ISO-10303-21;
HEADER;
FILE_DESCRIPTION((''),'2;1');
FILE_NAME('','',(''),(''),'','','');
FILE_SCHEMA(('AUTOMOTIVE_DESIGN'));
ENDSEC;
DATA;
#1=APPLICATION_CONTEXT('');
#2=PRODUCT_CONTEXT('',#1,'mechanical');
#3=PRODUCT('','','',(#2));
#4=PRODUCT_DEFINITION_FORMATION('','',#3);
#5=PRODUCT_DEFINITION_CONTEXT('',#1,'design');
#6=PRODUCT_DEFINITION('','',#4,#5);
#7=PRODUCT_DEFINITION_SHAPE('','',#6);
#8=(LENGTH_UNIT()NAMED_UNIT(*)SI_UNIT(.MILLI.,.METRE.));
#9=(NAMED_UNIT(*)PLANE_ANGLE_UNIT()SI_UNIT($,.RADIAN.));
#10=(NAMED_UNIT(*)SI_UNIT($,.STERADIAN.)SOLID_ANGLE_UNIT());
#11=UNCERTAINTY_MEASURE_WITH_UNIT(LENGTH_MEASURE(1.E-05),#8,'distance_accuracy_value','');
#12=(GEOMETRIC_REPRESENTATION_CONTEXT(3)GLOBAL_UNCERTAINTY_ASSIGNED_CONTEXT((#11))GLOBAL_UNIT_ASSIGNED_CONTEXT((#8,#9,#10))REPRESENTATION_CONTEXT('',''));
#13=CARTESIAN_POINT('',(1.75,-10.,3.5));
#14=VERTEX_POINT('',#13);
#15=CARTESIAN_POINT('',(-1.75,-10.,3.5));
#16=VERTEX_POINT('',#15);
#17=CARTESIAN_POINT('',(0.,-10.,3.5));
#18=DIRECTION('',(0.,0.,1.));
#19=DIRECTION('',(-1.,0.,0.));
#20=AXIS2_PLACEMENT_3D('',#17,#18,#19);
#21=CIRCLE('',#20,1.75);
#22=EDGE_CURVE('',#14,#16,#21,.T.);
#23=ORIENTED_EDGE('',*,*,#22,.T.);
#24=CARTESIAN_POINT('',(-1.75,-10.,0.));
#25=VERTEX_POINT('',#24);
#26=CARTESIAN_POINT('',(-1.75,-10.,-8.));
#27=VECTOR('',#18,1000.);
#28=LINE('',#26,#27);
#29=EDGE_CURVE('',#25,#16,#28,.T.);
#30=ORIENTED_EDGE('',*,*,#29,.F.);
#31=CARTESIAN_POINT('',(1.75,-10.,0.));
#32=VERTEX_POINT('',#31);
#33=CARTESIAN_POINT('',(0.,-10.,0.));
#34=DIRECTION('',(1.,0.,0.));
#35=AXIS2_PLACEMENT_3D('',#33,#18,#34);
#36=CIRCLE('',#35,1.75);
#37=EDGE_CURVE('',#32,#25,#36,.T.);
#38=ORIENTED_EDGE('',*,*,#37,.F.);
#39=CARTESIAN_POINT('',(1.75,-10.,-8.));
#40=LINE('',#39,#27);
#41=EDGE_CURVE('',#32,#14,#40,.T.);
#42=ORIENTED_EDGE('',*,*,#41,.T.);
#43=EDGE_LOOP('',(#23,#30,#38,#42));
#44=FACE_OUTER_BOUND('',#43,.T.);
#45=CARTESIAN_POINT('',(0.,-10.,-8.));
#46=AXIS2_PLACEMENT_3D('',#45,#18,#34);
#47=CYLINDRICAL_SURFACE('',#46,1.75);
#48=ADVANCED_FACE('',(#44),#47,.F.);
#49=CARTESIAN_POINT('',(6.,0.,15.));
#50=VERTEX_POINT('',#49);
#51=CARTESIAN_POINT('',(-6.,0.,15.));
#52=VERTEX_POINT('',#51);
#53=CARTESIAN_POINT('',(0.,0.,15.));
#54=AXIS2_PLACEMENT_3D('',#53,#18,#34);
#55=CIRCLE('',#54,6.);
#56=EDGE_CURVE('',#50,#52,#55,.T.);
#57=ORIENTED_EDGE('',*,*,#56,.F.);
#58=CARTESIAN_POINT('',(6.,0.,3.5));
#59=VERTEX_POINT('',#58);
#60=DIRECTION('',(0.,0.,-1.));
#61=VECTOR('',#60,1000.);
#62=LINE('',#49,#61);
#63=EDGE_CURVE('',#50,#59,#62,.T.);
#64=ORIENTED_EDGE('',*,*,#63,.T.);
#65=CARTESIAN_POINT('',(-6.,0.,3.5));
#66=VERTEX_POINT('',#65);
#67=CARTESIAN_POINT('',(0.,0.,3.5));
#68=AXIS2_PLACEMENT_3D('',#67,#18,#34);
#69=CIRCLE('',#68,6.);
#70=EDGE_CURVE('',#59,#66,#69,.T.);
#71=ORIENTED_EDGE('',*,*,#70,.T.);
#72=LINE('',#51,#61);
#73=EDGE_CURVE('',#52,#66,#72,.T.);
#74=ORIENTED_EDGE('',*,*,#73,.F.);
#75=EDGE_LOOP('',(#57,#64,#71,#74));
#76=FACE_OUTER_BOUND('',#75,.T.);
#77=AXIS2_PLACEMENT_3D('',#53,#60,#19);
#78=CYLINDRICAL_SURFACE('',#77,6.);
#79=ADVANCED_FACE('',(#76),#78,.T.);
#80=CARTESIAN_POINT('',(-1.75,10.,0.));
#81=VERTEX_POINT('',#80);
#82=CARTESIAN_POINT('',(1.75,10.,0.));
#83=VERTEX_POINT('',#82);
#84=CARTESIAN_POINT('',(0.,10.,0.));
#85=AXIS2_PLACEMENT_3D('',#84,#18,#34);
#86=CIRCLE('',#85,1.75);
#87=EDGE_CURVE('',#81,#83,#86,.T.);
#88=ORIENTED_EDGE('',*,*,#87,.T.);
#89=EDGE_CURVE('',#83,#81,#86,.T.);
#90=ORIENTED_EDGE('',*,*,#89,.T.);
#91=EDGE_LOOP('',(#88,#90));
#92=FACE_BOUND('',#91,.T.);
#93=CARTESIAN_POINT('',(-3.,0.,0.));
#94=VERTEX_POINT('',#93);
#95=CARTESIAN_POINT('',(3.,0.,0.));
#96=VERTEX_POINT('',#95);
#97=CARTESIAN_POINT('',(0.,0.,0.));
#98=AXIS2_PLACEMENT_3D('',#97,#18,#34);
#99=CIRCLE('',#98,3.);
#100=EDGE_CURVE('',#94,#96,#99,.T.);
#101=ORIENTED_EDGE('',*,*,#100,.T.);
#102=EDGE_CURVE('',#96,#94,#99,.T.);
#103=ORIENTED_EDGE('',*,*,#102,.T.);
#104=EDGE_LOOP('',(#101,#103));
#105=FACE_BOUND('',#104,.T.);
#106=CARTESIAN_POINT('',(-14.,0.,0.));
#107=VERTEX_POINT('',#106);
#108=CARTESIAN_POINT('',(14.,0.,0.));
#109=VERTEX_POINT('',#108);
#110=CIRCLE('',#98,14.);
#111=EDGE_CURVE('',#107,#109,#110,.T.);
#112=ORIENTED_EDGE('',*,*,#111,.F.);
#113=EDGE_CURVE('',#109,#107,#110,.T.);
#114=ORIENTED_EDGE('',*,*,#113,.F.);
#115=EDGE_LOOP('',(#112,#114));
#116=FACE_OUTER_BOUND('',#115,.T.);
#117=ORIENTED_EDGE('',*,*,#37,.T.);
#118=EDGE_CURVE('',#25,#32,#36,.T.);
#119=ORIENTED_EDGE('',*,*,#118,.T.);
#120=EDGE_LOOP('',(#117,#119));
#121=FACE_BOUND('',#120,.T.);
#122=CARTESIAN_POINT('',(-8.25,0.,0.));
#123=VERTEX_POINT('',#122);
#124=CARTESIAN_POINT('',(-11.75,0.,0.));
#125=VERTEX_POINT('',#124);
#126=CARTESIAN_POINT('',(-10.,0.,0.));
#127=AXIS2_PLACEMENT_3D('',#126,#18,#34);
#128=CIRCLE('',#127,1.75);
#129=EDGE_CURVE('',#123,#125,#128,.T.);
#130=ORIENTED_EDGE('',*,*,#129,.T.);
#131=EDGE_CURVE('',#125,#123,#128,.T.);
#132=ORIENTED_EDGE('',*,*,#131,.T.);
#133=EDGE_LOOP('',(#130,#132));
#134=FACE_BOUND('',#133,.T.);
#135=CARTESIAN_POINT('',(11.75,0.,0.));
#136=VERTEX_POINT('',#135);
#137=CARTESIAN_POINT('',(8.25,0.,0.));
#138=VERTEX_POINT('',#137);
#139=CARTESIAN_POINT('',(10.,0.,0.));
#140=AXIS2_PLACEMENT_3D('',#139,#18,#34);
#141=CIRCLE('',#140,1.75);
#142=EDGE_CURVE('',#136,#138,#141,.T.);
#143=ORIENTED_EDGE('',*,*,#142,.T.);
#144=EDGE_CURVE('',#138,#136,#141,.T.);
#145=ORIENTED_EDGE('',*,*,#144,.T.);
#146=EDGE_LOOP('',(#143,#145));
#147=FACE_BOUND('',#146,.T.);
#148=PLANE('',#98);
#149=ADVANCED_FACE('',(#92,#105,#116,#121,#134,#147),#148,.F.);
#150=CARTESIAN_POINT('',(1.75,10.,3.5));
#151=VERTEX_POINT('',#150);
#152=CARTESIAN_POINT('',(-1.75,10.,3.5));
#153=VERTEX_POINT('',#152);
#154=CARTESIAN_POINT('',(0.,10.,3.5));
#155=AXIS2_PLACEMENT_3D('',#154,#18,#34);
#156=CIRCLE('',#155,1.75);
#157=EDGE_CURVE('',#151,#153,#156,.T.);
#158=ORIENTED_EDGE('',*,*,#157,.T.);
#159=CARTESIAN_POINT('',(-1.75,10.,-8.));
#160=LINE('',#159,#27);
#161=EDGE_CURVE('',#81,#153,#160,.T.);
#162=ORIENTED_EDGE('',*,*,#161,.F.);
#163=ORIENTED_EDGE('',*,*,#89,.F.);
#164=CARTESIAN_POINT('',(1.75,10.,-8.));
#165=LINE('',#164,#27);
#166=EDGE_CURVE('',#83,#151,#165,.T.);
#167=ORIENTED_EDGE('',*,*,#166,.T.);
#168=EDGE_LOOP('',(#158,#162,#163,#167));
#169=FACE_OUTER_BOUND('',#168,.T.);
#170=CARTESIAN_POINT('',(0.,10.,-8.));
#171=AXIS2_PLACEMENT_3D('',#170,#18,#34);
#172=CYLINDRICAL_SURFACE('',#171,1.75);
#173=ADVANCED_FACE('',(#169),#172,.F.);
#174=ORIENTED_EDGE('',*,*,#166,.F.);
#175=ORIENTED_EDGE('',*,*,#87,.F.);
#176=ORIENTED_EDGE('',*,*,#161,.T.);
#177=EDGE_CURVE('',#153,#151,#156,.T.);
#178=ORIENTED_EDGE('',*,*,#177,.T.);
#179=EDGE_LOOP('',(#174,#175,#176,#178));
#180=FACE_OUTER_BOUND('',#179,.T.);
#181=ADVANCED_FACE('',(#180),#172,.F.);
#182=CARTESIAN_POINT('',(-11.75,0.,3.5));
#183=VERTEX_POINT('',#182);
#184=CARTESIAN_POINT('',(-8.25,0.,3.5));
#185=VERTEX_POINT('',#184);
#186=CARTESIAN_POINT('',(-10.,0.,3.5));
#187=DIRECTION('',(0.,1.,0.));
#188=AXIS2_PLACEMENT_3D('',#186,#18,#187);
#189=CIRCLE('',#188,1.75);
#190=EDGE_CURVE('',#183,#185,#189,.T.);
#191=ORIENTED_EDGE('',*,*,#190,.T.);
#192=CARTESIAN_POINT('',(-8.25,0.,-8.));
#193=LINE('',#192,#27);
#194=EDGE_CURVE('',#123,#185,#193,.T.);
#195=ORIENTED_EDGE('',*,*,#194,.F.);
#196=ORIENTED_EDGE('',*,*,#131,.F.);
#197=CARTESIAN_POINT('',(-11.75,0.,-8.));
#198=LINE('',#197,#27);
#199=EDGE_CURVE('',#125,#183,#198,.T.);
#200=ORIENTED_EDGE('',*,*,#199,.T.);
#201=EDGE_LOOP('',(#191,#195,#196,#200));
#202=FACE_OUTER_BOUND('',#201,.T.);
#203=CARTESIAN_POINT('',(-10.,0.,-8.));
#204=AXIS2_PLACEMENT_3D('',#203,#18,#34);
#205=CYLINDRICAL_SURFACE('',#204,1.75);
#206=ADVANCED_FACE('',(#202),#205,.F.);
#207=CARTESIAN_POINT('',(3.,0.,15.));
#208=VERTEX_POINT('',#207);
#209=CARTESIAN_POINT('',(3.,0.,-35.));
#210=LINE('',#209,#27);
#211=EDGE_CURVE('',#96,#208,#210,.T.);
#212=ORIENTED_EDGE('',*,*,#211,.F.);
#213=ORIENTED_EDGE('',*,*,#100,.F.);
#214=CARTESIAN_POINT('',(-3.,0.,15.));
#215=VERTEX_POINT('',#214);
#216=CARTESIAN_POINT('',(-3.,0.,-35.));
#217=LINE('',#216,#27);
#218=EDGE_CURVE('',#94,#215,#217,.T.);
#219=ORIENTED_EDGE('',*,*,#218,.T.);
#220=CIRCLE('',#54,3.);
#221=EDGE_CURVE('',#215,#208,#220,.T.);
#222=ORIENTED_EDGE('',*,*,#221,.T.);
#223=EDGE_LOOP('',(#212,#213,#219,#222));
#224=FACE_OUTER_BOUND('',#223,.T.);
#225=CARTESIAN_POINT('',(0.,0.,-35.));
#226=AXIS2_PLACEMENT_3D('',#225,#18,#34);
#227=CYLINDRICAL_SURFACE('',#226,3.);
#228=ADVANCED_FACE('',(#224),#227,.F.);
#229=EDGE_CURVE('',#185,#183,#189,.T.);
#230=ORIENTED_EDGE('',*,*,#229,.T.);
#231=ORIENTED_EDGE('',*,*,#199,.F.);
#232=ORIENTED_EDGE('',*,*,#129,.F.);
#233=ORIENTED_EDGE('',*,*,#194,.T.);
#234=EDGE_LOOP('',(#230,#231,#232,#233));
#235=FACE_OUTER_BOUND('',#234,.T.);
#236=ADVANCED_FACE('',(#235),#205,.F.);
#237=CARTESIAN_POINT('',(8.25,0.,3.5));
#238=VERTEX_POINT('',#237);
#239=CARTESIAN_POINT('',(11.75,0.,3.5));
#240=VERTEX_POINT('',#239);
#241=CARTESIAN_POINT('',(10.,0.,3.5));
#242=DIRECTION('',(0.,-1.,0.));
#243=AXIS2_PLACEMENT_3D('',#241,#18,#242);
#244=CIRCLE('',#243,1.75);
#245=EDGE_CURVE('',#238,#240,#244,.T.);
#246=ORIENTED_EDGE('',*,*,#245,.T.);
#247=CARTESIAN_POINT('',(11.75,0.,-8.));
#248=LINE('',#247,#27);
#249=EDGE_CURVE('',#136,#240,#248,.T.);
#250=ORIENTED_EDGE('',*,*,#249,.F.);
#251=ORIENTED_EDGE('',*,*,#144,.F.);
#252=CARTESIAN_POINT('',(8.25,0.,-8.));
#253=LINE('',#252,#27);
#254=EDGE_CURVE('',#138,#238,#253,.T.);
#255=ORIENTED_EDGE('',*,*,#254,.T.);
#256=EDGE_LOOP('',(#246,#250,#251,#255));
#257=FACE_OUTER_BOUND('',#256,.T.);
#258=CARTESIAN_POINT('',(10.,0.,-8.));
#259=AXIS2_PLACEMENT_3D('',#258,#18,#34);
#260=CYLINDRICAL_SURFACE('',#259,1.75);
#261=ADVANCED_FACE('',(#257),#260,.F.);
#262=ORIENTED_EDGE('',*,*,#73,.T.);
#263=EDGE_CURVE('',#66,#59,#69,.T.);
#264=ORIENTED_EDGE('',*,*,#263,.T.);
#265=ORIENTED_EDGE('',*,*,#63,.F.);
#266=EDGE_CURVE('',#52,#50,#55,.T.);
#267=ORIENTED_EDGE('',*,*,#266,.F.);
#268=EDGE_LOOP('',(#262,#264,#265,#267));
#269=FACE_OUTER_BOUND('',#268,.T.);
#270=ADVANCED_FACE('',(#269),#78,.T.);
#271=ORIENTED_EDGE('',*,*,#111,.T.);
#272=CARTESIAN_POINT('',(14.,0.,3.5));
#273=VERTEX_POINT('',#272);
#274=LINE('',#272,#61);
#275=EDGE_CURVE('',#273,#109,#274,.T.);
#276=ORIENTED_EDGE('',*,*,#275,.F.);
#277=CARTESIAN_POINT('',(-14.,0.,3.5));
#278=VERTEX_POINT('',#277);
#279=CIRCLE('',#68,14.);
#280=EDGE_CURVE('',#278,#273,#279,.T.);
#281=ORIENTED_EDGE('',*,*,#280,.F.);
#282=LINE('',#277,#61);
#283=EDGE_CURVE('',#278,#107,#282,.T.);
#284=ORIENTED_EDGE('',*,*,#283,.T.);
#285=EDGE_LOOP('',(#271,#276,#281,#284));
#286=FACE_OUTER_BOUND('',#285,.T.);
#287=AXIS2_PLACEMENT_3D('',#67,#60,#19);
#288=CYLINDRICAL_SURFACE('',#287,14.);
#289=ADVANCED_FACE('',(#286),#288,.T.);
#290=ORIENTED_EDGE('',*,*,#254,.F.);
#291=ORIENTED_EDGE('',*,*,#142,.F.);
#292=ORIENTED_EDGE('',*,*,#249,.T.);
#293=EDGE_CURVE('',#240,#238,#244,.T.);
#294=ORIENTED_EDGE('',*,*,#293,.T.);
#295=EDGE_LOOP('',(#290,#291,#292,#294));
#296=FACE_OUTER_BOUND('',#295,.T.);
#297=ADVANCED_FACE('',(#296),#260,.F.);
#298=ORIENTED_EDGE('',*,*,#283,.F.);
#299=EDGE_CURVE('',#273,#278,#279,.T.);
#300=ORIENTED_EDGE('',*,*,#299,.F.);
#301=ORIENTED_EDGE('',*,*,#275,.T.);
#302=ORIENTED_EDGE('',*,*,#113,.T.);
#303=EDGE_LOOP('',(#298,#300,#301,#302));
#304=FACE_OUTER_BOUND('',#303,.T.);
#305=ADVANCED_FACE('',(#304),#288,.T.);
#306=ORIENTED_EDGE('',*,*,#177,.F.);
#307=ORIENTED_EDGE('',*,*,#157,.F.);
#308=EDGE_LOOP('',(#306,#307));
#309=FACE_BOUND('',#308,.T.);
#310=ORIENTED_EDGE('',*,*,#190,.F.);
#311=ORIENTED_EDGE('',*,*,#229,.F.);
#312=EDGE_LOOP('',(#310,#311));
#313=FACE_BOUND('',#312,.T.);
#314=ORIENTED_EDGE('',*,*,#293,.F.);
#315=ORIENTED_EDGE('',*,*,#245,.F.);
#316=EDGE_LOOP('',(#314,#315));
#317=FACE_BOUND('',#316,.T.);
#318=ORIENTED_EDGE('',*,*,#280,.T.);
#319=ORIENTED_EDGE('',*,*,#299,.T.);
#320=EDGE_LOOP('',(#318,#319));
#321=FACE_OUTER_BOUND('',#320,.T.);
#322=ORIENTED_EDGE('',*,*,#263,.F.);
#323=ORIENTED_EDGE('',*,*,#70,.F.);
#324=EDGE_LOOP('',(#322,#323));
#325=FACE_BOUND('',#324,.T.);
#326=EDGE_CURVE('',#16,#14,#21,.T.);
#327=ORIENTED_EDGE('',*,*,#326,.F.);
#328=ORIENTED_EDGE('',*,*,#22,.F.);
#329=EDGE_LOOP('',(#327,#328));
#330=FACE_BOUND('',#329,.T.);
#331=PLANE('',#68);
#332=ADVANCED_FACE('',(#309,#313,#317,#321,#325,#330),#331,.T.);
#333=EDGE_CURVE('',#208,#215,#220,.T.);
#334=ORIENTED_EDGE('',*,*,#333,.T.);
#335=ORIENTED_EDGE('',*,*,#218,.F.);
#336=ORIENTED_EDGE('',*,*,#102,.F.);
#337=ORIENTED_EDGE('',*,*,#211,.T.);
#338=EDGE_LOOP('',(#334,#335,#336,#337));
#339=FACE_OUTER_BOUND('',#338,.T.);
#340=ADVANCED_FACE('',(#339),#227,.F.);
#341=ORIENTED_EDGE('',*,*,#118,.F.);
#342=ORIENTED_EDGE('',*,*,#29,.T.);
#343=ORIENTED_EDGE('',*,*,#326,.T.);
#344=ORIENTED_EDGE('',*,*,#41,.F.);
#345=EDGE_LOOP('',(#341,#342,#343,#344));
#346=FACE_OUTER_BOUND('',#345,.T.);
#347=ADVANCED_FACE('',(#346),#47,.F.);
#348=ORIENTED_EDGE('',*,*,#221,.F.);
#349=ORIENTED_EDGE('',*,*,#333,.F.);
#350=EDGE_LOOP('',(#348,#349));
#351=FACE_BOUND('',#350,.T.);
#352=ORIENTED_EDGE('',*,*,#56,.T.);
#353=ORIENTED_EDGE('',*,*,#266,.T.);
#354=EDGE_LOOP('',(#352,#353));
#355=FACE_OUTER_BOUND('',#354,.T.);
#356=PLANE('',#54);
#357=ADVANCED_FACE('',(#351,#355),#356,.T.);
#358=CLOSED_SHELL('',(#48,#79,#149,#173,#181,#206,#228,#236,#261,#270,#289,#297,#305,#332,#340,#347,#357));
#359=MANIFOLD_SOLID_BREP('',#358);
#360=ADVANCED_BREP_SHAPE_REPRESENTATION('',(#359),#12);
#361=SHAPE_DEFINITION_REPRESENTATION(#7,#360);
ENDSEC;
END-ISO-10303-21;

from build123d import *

# Parameters (mm, degrees)
SKETCH1_R           = 14
BOSS_EXTRUDE1_DEPTH = 3.5
SKETCH2_R           = 6
BOSS_EXTRUDE2_DEPTH = 11.5
SKETCH3_R           = 1.75
CUT_EXTRUDE1_DEPTH  = 11.5
CIRPATTERN1_COUNT   = 4
SKETCH4_R           = 3
CUT_EXTRUDE2_DEPTH  = 50


with BuildPart() as part:
    # Sketch1 → Boss-Extrude1 (new body)
    with BuildSketch(Plane.XY):
        Circle(SKETCH1_R)
    extrude(amount=BOSS_EXTRUDE1_DEPTH)

    # Sketch2 → Boss-Extrude2 (add)
    with BuildSketch(Plane.XY.offset(3.5)):
        Circle(SKETCH2_R)
    extrude(amount=BOSS_EXTRUDE2_DEPTH)

    # Sketch3 → Cut-Extrude1 (cut)
    with BuildSketch(Plane.XY.offset(3.5)):
        with Locations((0, 10)):
            Circle(SKETCH3_R)
    cut_extrude1 = extrude(amount=-CUT_EXTRUDE1_DEPTH, mode=Mode.SUBTRACT)

    # CirPattern1: Cut-Extrude1 ×4 about axis
    cirpattern1_axis = Axis((0, 0, 0), (0, 0, 1))
    for i in range(1, CIRPATTERN1_COUNT):
        add(cut_extrude1.rotate(cirpattern1_axis, i * 360 / CIRPATTERN1_COUNT), mode=Mode.SUBTRACT)

    # Sketch4 → Cut-Extrude2 (cut)
    with BuildSketch(Plane.XY.offset(15)):
        Circle(SKETCH4_R)
    extrude(amount=-CUT_EXTRUDE2_DEPTH, mode=Mode.SUBTRACT)


solid = part.part
